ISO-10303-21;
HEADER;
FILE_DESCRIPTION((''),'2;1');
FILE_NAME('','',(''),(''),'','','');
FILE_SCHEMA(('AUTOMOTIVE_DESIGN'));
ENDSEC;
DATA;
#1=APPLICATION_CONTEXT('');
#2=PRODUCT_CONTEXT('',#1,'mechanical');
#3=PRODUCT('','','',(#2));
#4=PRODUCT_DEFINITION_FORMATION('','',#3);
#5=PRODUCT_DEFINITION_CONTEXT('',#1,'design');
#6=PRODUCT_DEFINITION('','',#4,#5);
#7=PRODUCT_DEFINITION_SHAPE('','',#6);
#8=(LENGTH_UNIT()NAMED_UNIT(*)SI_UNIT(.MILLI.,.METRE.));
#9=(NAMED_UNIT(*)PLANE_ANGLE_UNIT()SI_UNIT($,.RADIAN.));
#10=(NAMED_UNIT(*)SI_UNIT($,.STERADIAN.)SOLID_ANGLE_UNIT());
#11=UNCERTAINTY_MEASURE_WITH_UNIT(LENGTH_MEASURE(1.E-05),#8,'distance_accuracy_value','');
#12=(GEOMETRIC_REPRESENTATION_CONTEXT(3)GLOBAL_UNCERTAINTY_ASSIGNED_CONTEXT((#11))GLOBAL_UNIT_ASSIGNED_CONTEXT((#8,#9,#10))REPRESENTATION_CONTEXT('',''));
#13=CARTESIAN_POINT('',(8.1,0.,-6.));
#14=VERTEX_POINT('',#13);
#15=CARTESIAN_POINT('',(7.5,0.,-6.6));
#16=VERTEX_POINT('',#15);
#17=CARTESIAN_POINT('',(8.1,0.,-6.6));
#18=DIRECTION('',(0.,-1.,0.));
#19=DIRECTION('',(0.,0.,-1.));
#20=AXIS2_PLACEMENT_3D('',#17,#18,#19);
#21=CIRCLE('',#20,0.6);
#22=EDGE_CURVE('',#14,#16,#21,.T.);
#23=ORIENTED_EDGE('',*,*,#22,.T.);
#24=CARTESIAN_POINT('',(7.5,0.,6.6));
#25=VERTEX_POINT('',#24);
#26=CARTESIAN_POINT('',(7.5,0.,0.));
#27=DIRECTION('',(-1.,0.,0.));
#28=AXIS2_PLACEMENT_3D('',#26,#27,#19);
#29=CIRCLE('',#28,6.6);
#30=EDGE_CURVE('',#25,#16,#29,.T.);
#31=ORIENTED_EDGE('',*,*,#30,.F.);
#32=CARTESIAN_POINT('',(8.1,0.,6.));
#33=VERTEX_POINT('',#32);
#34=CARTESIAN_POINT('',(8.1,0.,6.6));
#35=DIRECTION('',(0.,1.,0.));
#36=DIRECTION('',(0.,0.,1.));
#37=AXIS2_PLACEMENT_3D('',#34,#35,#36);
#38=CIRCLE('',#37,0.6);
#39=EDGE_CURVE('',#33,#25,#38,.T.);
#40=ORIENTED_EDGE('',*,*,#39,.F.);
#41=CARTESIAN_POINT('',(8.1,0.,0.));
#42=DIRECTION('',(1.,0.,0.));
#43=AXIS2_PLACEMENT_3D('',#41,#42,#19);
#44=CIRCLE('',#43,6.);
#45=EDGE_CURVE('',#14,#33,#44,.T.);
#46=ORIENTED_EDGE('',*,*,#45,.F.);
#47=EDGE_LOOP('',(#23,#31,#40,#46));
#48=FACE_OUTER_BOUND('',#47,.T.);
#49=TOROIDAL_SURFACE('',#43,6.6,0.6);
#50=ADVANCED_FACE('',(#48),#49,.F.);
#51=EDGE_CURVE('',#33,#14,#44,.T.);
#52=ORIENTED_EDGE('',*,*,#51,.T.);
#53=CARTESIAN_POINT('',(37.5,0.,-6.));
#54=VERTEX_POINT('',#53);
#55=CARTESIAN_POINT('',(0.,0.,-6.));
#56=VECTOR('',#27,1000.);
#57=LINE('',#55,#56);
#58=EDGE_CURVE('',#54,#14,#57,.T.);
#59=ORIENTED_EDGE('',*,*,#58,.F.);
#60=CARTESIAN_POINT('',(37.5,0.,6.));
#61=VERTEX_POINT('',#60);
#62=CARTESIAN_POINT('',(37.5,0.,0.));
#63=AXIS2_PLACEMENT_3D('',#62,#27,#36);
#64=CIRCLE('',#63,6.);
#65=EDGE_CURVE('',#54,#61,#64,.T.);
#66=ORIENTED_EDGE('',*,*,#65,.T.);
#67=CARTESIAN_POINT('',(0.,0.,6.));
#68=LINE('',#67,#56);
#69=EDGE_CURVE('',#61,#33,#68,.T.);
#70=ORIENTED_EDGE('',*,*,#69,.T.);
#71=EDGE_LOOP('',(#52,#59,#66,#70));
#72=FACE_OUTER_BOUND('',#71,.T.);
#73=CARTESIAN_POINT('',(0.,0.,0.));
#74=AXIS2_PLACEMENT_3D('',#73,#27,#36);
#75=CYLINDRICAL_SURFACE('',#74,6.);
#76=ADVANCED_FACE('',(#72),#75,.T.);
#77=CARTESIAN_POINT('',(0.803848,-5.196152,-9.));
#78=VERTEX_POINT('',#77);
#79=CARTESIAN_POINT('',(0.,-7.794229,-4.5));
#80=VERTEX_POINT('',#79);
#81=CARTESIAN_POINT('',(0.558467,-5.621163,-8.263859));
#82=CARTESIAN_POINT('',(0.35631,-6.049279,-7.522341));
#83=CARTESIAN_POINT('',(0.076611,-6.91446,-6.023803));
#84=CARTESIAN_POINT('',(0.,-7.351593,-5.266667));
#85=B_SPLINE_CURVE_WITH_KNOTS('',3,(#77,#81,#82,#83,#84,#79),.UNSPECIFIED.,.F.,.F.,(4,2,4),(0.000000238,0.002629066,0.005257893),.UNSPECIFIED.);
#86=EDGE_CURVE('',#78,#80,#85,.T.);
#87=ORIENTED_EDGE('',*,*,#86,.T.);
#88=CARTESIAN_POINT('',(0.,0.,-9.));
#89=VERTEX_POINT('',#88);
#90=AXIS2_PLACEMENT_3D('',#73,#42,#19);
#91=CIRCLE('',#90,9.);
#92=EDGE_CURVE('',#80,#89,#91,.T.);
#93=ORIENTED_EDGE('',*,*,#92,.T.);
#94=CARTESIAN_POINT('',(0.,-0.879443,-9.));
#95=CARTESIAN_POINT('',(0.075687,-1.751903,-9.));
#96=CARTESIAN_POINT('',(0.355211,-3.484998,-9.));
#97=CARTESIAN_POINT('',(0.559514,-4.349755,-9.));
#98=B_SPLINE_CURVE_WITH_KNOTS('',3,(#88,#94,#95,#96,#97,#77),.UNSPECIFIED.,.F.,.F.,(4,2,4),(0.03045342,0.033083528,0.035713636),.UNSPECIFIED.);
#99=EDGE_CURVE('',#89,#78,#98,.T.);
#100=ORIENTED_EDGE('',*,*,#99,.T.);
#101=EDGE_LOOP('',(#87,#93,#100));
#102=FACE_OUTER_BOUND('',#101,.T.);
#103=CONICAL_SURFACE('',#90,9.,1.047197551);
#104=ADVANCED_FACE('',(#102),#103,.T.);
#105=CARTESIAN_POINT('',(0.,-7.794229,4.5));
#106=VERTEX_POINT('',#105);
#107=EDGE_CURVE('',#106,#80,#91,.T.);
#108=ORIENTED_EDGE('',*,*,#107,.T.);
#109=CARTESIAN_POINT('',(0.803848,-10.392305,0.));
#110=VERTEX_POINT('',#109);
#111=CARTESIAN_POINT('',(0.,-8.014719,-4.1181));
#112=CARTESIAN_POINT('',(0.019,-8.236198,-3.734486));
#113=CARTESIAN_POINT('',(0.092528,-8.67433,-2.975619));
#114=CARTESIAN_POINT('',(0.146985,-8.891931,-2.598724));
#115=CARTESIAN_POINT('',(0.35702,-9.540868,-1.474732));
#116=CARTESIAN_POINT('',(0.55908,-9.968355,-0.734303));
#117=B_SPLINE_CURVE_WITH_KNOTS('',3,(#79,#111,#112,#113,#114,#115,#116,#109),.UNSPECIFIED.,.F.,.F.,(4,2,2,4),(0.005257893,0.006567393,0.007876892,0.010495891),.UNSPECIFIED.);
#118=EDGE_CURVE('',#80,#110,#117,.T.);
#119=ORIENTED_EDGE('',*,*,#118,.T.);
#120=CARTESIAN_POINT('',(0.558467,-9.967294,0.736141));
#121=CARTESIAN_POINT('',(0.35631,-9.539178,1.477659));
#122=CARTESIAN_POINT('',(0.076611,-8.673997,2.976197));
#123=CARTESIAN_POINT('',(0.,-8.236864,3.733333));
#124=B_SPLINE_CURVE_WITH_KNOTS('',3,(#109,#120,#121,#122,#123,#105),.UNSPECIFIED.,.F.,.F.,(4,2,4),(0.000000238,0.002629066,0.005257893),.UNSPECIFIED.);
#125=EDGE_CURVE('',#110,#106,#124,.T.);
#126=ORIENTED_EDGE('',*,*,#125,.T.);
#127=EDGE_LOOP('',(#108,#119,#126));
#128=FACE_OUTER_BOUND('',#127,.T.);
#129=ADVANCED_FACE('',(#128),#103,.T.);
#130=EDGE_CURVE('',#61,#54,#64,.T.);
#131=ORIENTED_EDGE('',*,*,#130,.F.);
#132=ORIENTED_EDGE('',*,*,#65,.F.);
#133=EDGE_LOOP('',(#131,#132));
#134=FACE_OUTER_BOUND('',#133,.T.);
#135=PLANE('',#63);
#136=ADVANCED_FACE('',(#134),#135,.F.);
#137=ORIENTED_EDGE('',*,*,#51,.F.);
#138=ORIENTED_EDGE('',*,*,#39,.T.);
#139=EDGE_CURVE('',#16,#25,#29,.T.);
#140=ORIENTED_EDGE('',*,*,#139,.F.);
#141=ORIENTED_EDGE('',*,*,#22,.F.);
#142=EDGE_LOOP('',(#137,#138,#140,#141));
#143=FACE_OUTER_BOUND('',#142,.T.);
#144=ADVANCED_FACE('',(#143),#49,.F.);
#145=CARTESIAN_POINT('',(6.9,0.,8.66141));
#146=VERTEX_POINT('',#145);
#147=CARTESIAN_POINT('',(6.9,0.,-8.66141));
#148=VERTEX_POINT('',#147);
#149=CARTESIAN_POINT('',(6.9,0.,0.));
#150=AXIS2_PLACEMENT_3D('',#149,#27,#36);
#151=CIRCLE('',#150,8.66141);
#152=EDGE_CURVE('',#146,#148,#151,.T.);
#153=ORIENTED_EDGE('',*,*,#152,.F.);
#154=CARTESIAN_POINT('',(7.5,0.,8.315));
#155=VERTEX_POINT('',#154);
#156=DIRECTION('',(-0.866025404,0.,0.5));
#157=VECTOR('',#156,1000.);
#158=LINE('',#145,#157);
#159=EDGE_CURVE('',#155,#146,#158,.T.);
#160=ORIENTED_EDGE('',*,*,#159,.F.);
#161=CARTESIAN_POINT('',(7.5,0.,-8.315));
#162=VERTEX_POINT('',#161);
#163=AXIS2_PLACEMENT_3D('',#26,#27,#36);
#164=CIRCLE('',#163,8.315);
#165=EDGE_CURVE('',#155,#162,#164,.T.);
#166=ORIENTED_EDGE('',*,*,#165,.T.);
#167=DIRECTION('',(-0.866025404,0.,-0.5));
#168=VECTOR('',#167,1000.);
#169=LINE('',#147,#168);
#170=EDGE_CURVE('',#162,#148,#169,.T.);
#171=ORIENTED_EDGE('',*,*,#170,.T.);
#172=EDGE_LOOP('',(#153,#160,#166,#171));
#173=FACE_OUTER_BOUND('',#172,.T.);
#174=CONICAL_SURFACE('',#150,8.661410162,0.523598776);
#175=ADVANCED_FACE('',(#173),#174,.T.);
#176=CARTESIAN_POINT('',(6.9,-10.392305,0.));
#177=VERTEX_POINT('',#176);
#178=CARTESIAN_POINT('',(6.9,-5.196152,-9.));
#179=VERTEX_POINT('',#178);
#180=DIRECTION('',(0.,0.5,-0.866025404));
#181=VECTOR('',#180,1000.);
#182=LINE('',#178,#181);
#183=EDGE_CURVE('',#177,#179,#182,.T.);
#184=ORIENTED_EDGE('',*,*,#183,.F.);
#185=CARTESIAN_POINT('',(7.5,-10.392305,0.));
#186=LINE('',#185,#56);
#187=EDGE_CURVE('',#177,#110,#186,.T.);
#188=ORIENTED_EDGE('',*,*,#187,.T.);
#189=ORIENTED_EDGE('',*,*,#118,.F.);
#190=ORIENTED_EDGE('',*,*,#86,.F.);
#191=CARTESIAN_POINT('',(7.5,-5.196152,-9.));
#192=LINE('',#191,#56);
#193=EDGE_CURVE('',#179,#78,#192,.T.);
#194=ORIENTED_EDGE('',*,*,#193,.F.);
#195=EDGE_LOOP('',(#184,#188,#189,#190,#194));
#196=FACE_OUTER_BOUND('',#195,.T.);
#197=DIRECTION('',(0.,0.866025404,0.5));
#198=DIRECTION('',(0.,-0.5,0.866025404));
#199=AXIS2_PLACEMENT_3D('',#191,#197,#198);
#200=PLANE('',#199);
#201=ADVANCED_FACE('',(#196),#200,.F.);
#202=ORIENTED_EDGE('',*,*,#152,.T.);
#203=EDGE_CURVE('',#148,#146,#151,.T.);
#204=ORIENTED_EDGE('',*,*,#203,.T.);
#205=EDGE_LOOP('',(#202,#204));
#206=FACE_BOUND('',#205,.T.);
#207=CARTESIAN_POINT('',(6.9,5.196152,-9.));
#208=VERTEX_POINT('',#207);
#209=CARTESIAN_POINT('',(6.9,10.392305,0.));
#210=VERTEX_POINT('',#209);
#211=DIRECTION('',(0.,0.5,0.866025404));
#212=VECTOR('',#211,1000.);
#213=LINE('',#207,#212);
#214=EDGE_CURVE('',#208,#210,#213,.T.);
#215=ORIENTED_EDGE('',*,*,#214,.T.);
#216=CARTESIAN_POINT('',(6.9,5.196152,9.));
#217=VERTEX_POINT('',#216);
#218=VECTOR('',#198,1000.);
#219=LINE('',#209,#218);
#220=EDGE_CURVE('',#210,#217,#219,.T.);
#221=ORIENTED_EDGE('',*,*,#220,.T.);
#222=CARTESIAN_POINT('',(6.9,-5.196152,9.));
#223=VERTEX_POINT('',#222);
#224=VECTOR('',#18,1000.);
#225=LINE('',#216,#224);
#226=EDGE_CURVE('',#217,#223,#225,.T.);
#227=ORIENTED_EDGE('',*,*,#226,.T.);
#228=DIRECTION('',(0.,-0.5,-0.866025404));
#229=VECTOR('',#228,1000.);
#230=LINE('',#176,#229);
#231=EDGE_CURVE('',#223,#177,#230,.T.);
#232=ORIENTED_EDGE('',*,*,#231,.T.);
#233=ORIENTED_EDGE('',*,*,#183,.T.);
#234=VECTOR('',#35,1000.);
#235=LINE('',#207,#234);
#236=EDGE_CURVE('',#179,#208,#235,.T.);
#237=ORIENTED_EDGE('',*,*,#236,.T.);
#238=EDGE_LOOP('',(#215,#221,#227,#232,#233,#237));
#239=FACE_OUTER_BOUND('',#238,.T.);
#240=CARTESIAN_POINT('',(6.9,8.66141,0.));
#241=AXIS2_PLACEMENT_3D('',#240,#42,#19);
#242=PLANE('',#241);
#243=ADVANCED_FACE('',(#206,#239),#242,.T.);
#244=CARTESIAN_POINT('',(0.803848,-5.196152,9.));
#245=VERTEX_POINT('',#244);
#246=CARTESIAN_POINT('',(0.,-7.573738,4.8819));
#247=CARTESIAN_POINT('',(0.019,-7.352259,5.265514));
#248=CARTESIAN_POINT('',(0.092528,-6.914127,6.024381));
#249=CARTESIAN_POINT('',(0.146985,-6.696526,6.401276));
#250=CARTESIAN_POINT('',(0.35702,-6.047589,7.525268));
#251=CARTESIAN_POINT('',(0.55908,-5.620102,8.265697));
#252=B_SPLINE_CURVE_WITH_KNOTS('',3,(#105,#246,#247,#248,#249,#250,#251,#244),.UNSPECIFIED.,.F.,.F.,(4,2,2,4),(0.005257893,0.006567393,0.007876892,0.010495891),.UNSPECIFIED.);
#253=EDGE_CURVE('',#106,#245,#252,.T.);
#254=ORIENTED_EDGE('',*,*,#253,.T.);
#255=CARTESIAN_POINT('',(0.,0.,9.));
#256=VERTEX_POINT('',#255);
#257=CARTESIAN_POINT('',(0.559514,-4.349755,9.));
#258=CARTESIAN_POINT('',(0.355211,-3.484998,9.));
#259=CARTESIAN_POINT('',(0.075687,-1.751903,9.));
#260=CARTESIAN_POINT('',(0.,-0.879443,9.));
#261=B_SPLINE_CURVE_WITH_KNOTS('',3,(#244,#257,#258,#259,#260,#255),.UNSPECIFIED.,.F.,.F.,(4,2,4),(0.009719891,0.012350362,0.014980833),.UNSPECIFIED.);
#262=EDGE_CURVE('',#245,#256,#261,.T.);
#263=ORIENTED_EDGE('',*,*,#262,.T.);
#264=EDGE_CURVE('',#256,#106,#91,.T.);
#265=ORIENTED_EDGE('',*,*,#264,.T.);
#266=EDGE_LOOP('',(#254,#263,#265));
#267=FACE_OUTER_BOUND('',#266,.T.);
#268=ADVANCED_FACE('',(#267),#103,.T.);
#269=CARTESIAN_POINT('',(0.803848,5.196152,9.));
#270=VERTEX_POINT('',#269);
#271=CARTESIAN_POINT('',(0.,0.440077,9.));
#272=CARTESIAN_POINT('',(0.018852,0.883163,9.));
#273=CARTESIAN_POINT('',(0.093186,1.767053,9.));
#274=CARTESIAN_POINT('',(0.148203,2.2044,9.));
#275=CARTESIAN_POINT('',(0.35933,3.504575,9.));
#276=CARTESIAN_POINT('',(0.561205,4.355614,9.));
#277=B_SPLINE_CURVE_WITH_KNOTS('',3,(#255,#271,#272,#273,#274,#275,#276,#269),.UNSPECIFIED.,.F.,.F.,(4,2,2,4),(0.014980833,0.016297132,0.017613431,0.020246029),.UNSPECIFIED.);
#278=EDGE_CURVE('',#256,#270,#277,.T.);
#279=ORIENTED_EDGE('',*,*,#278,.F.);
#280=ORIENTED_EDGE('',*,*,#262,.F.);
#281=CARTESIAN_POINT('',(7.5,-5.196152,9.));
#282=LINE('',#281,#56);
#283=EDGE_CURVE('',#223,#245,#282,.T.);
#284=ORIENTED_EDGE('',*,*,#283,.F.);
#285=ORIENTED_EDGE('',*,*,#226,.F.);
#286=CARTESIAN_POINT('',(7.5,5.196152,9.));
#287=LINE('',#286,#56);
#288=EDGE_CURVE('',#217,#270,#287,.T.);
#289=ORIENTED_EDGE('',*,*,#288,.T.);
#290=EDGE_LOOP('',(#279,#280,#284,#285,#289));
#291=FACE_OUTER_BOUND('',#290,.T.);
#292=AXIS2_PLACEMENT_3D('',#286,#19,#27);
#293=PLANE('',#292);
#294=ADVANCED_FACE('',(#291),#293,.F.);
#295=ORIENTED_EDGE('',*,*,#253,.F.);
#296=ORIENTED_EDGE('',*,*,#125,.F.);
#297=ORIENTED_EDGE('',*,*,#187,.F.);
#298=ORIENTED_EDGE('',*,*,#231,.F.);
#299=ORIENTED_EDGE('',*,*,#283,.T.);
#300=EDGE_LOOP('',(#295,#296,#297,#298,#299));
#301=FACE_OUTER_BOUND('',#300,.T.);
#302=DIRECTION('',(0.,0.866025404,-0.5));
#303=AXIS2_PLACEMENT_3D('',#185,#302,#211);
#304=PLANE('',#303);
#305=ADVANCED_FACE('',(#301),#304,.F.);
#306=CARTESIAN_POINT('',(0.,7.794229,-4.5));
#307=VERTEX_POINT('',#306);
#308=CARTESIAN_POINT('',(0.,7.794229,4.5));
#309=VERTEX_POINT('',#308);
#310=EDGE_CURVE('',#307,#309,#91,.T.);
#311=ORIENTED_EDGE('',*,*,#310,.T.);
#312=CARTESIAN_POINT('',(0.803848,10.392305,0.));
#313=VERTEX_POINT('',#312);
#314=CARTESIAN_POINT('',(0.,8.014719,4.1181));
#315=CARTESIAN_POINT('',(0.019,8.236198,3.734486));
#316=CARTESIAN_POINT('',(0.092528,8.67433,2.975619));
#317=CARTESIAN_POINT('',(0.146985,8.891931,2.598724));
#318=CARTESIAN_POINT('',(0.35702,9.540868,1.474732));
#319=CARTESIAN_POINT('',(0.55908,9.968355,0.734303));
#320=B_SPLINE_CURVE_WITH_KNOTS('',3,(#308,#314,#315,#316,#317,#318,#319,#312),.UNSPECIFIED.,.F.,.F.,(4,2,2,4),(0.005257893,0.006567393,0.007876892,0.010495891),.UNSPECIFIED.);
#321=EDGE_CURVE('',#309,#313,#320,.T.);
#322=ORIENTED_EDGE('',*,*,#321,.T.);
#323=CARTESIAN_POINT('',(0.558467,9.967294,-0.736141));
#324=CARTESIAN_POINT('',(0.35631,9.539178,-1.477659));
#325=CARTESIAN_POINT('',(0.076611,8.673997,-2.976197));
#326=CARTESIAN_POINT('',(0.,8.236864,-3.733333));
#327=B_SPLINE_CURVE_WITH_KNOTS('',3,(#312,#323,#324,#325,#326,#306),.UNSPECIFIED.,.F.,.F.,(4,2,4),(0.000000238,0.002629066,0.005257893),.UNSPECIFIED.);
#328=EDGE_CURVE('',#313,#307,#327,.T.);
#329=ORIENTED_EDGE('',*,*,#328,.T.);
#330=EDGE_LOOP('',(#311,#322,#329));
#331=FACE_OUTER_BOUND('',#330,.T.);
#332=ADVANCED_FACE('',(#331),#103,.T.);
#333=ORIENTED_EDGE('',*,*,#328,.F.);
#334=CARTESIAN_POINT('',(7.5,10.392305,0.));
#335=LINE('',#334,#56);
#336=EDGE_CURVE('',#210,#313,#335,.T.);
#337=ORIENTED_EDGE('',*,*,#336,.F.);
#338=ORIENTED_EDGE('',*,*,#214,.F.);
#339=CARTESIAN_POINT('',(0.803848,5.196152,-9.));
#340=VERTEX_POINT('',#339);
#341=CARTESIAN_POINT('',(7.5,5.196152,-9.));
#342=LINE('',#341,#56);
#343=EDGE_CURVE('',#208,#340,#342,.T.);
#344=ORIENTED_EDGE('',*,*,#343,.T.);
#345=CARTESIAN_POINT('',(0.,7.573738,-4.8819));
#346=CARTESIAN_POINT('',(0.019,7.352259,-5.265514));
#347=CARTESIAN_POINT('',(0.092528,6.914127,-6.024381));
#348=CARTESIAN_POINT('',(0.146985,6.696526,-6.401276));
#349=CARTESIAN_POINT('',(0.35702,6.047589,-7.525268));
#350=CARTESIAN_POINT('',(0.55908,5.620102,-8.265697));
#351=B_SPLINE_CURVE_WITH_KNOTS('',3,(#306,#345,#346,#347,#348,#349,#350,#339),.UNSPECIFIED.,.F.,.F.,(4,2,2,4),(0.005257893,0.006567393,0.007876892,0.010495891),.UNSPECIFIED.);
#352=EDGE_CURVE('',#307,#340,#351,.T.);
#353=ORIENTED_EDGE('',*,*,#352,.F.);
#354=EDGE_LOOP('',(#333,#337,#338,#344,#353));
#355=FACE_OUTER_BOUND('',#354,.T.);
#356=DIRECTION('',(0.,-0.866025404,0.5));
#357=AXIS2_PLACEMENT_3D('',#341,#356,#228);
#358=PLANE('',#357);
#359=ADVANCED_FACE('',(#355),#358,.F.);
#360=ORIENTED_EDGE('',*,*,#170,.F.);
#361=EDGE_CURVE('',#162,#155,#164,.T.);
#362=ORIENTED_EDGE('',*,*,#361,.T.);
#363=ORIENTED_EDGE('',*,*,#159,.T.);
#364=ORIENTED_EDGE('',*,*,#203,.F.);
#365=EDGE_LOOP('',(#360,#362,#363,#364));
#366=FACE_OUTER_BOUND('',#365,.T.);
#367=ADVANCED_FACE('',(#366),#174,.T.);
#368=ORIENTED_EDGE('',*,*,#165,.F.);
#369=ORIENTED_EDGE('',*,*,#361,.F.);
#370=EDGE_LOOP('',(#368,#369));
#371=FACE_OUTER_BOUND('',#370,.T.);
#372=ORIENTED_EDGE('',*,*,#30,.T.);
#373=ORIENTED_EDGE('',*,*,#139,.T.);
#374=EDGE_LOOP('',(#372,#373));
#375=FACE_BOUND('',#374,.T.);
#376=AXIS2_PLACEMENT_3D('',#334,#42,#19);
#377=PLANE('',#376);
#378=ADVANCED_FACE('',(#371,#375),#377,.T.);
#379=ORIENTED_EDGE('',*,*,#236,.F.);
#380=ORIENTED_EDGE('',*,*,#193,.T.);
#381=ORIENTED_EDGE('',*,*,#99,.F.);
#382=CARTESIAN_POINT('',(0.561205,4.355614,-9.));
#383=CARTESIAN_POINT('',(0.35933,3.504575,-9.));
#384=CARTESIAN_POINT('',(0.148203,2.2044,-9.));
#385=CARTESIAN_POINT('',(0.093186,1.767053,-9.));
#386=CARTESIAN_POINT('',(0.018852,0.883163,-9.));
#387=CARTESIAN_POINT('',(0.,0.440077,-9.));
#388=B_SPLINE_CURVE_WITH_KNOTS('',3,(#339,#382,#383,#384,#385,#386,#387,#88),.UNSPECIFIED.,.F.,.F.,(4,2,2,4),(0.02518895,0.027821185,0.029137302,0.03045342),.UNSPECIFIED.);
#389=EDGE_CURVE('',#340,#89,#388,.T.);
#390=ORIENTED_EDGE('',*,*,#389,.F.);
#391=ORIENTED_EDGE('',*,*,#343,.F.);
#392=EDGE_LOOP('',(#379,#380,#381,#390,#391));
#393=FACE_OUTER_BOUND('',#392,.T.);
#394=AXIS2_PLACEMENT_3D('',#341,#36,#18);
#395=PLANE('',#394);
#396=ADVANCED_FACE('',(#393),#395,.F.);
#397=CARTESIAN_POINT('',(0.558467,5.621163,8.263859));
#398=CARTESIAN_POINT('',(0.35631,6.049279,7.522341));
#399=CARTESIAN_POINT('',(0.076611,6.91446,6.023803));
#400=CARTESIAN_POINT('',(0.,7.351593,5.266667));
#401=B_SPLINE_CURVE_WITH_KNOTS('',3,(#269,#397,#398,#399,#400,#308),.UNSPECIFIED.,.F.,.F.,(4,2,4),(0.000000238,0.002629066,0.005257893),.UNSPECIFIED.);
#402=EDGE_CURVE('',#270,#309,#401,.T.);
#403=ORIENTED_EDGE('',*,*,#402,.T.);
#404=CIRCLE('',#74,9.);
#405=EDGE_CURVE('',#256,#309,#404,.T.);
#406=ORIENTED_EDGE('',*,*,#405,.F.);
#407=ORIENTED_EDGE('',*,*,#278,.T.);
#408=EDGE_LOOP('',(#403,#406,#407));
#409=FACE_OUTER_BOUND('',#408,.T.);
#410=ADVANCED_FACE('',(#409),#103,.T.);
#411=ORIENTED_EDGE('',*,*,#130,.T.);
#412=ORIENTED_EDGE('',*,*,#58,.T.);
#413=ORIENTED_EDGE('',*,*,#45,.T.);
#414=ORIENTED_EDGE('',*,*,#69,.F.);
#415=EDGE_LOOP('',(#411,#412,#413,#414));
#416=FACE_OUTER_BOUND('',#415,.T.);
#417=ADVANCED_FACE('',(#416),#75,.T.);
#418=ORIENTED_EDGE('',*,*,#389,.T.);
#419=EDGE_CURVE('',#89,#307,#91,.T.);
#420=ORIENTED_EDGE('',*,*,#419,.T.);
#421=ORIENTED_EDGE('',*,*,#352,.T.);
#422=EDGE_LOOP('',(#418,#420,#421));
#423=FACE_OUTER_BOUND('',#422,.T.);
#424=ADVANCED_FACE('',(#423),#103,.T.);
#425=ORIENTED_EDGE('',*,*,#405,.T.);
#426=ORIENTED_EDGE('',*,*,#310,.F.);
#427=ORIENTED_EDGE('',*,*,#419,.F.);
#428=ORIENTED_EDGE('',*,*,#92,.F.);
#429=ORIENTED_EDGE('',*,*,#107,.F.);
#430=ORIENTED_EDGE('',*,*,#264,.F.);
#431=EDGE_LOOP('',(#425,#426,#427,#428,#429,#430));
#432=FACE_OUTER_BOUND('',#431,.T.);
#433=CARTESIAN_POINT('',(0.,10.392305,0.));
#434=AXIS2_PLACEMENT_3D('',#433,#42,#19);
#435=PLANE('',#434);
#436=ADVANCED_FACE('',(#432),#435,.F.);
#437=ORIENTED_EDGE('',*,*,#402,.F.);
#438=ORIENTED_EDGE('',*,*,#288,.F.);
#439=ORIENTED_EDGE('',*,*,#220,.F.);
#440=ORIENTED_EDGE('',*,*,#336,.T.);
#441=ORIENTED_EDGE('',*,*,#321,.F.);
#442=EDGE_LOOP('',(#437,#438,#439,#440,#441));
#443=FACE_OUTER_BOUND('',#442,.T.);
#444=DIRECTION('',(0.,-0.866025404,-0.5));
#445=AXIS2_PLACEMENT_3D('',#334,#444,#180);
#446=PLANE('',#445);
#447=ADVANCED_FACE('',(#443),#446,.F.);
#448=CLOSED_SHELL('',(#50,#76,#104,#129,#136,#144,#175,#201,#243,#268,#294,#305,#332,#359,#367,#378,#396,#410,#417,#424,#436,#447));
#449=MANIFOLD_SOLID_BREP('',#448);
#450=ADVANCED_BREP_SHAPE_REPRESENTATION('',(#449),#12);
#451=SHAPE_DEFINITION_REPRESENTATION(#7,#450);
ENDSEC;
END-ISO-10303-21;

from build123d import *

# Parameters (mm, degrees)
EXTRUDE_387_DEPTH = 7.5
FILLET_1280_R     = 0.6


with BuildPart() as part:
    # 草图1 → Extrude 387 (new body)
    with BuildSketch(Plane(origin=(0, 0, 0), x_dir=(0, 0, -1), z_dir=(1, 0, 0))):
        Polygon((9, 5.196152423), (9, -5.196152423), (0, -10.392304845), (-9, -5.196152423), (-9, 5.196152423), (0, 10.392304845), align=None)
    extrude(amount=EXTRUDE_387_DEPTH)

    # 草图2 → 凸台-旋转1 (revolve)
    with BuildSketch(Plane.XY, mode=Mode.PRIVATE) as revolve_1_sk:
        Polygon((0, 0), (37.5, 0), (37.5, 4.4845), (37.5, 6), (7.5, 6), (0, 6), align=None)
    revolve(revolve_1_sk.sketch.rotate(Axis((0, 0, 0), (1, 0, 0)), 90), axis=Axis((0, 0, 0), (1, 0, 0)))

    # 草图3 → 切除-旋转1 (revolve, cut)
    with BuildSketch(Plane.XY):
        Polygon((0, 9), (3.690598923, 15.392304845), (3.690598923, 20.392304845), (-10, 20.392304845), (-10, 9), align=None)
    revolve(axis=Axis((0, 0, 0), (1, 0, 0)), mode=Mode.SUBTRACT)

    # 草图4 → 切除-旋转3 (revolve, cut)
    with BuildSketch(Plane.XY, mode=Mode.PRIVATE) as cut_revolve_3_sk:
        Polygon((7.5, 8.315), (6.9, 8.661410162), (6.9, 10.392304845), (7.5, 10.392304845), align=None)
    revolve(cut_revolve_3_sk.sketch.rotate(Axis((0, 0, 0), (1, 0, 0)), 90), axis=Axis((0, 0, 0), (1, 0, 0)), mode=Mode.SUBTRACT)

    # Fillet 1280
    fillet_1280_edges = [part.edges().sort_by_distance(p)[0] for p in [
        (7.5, 0, -6),
    ]]
    fillet(fillet_1280_edges, radius=FILLET_1280_R)


solid = part.part
